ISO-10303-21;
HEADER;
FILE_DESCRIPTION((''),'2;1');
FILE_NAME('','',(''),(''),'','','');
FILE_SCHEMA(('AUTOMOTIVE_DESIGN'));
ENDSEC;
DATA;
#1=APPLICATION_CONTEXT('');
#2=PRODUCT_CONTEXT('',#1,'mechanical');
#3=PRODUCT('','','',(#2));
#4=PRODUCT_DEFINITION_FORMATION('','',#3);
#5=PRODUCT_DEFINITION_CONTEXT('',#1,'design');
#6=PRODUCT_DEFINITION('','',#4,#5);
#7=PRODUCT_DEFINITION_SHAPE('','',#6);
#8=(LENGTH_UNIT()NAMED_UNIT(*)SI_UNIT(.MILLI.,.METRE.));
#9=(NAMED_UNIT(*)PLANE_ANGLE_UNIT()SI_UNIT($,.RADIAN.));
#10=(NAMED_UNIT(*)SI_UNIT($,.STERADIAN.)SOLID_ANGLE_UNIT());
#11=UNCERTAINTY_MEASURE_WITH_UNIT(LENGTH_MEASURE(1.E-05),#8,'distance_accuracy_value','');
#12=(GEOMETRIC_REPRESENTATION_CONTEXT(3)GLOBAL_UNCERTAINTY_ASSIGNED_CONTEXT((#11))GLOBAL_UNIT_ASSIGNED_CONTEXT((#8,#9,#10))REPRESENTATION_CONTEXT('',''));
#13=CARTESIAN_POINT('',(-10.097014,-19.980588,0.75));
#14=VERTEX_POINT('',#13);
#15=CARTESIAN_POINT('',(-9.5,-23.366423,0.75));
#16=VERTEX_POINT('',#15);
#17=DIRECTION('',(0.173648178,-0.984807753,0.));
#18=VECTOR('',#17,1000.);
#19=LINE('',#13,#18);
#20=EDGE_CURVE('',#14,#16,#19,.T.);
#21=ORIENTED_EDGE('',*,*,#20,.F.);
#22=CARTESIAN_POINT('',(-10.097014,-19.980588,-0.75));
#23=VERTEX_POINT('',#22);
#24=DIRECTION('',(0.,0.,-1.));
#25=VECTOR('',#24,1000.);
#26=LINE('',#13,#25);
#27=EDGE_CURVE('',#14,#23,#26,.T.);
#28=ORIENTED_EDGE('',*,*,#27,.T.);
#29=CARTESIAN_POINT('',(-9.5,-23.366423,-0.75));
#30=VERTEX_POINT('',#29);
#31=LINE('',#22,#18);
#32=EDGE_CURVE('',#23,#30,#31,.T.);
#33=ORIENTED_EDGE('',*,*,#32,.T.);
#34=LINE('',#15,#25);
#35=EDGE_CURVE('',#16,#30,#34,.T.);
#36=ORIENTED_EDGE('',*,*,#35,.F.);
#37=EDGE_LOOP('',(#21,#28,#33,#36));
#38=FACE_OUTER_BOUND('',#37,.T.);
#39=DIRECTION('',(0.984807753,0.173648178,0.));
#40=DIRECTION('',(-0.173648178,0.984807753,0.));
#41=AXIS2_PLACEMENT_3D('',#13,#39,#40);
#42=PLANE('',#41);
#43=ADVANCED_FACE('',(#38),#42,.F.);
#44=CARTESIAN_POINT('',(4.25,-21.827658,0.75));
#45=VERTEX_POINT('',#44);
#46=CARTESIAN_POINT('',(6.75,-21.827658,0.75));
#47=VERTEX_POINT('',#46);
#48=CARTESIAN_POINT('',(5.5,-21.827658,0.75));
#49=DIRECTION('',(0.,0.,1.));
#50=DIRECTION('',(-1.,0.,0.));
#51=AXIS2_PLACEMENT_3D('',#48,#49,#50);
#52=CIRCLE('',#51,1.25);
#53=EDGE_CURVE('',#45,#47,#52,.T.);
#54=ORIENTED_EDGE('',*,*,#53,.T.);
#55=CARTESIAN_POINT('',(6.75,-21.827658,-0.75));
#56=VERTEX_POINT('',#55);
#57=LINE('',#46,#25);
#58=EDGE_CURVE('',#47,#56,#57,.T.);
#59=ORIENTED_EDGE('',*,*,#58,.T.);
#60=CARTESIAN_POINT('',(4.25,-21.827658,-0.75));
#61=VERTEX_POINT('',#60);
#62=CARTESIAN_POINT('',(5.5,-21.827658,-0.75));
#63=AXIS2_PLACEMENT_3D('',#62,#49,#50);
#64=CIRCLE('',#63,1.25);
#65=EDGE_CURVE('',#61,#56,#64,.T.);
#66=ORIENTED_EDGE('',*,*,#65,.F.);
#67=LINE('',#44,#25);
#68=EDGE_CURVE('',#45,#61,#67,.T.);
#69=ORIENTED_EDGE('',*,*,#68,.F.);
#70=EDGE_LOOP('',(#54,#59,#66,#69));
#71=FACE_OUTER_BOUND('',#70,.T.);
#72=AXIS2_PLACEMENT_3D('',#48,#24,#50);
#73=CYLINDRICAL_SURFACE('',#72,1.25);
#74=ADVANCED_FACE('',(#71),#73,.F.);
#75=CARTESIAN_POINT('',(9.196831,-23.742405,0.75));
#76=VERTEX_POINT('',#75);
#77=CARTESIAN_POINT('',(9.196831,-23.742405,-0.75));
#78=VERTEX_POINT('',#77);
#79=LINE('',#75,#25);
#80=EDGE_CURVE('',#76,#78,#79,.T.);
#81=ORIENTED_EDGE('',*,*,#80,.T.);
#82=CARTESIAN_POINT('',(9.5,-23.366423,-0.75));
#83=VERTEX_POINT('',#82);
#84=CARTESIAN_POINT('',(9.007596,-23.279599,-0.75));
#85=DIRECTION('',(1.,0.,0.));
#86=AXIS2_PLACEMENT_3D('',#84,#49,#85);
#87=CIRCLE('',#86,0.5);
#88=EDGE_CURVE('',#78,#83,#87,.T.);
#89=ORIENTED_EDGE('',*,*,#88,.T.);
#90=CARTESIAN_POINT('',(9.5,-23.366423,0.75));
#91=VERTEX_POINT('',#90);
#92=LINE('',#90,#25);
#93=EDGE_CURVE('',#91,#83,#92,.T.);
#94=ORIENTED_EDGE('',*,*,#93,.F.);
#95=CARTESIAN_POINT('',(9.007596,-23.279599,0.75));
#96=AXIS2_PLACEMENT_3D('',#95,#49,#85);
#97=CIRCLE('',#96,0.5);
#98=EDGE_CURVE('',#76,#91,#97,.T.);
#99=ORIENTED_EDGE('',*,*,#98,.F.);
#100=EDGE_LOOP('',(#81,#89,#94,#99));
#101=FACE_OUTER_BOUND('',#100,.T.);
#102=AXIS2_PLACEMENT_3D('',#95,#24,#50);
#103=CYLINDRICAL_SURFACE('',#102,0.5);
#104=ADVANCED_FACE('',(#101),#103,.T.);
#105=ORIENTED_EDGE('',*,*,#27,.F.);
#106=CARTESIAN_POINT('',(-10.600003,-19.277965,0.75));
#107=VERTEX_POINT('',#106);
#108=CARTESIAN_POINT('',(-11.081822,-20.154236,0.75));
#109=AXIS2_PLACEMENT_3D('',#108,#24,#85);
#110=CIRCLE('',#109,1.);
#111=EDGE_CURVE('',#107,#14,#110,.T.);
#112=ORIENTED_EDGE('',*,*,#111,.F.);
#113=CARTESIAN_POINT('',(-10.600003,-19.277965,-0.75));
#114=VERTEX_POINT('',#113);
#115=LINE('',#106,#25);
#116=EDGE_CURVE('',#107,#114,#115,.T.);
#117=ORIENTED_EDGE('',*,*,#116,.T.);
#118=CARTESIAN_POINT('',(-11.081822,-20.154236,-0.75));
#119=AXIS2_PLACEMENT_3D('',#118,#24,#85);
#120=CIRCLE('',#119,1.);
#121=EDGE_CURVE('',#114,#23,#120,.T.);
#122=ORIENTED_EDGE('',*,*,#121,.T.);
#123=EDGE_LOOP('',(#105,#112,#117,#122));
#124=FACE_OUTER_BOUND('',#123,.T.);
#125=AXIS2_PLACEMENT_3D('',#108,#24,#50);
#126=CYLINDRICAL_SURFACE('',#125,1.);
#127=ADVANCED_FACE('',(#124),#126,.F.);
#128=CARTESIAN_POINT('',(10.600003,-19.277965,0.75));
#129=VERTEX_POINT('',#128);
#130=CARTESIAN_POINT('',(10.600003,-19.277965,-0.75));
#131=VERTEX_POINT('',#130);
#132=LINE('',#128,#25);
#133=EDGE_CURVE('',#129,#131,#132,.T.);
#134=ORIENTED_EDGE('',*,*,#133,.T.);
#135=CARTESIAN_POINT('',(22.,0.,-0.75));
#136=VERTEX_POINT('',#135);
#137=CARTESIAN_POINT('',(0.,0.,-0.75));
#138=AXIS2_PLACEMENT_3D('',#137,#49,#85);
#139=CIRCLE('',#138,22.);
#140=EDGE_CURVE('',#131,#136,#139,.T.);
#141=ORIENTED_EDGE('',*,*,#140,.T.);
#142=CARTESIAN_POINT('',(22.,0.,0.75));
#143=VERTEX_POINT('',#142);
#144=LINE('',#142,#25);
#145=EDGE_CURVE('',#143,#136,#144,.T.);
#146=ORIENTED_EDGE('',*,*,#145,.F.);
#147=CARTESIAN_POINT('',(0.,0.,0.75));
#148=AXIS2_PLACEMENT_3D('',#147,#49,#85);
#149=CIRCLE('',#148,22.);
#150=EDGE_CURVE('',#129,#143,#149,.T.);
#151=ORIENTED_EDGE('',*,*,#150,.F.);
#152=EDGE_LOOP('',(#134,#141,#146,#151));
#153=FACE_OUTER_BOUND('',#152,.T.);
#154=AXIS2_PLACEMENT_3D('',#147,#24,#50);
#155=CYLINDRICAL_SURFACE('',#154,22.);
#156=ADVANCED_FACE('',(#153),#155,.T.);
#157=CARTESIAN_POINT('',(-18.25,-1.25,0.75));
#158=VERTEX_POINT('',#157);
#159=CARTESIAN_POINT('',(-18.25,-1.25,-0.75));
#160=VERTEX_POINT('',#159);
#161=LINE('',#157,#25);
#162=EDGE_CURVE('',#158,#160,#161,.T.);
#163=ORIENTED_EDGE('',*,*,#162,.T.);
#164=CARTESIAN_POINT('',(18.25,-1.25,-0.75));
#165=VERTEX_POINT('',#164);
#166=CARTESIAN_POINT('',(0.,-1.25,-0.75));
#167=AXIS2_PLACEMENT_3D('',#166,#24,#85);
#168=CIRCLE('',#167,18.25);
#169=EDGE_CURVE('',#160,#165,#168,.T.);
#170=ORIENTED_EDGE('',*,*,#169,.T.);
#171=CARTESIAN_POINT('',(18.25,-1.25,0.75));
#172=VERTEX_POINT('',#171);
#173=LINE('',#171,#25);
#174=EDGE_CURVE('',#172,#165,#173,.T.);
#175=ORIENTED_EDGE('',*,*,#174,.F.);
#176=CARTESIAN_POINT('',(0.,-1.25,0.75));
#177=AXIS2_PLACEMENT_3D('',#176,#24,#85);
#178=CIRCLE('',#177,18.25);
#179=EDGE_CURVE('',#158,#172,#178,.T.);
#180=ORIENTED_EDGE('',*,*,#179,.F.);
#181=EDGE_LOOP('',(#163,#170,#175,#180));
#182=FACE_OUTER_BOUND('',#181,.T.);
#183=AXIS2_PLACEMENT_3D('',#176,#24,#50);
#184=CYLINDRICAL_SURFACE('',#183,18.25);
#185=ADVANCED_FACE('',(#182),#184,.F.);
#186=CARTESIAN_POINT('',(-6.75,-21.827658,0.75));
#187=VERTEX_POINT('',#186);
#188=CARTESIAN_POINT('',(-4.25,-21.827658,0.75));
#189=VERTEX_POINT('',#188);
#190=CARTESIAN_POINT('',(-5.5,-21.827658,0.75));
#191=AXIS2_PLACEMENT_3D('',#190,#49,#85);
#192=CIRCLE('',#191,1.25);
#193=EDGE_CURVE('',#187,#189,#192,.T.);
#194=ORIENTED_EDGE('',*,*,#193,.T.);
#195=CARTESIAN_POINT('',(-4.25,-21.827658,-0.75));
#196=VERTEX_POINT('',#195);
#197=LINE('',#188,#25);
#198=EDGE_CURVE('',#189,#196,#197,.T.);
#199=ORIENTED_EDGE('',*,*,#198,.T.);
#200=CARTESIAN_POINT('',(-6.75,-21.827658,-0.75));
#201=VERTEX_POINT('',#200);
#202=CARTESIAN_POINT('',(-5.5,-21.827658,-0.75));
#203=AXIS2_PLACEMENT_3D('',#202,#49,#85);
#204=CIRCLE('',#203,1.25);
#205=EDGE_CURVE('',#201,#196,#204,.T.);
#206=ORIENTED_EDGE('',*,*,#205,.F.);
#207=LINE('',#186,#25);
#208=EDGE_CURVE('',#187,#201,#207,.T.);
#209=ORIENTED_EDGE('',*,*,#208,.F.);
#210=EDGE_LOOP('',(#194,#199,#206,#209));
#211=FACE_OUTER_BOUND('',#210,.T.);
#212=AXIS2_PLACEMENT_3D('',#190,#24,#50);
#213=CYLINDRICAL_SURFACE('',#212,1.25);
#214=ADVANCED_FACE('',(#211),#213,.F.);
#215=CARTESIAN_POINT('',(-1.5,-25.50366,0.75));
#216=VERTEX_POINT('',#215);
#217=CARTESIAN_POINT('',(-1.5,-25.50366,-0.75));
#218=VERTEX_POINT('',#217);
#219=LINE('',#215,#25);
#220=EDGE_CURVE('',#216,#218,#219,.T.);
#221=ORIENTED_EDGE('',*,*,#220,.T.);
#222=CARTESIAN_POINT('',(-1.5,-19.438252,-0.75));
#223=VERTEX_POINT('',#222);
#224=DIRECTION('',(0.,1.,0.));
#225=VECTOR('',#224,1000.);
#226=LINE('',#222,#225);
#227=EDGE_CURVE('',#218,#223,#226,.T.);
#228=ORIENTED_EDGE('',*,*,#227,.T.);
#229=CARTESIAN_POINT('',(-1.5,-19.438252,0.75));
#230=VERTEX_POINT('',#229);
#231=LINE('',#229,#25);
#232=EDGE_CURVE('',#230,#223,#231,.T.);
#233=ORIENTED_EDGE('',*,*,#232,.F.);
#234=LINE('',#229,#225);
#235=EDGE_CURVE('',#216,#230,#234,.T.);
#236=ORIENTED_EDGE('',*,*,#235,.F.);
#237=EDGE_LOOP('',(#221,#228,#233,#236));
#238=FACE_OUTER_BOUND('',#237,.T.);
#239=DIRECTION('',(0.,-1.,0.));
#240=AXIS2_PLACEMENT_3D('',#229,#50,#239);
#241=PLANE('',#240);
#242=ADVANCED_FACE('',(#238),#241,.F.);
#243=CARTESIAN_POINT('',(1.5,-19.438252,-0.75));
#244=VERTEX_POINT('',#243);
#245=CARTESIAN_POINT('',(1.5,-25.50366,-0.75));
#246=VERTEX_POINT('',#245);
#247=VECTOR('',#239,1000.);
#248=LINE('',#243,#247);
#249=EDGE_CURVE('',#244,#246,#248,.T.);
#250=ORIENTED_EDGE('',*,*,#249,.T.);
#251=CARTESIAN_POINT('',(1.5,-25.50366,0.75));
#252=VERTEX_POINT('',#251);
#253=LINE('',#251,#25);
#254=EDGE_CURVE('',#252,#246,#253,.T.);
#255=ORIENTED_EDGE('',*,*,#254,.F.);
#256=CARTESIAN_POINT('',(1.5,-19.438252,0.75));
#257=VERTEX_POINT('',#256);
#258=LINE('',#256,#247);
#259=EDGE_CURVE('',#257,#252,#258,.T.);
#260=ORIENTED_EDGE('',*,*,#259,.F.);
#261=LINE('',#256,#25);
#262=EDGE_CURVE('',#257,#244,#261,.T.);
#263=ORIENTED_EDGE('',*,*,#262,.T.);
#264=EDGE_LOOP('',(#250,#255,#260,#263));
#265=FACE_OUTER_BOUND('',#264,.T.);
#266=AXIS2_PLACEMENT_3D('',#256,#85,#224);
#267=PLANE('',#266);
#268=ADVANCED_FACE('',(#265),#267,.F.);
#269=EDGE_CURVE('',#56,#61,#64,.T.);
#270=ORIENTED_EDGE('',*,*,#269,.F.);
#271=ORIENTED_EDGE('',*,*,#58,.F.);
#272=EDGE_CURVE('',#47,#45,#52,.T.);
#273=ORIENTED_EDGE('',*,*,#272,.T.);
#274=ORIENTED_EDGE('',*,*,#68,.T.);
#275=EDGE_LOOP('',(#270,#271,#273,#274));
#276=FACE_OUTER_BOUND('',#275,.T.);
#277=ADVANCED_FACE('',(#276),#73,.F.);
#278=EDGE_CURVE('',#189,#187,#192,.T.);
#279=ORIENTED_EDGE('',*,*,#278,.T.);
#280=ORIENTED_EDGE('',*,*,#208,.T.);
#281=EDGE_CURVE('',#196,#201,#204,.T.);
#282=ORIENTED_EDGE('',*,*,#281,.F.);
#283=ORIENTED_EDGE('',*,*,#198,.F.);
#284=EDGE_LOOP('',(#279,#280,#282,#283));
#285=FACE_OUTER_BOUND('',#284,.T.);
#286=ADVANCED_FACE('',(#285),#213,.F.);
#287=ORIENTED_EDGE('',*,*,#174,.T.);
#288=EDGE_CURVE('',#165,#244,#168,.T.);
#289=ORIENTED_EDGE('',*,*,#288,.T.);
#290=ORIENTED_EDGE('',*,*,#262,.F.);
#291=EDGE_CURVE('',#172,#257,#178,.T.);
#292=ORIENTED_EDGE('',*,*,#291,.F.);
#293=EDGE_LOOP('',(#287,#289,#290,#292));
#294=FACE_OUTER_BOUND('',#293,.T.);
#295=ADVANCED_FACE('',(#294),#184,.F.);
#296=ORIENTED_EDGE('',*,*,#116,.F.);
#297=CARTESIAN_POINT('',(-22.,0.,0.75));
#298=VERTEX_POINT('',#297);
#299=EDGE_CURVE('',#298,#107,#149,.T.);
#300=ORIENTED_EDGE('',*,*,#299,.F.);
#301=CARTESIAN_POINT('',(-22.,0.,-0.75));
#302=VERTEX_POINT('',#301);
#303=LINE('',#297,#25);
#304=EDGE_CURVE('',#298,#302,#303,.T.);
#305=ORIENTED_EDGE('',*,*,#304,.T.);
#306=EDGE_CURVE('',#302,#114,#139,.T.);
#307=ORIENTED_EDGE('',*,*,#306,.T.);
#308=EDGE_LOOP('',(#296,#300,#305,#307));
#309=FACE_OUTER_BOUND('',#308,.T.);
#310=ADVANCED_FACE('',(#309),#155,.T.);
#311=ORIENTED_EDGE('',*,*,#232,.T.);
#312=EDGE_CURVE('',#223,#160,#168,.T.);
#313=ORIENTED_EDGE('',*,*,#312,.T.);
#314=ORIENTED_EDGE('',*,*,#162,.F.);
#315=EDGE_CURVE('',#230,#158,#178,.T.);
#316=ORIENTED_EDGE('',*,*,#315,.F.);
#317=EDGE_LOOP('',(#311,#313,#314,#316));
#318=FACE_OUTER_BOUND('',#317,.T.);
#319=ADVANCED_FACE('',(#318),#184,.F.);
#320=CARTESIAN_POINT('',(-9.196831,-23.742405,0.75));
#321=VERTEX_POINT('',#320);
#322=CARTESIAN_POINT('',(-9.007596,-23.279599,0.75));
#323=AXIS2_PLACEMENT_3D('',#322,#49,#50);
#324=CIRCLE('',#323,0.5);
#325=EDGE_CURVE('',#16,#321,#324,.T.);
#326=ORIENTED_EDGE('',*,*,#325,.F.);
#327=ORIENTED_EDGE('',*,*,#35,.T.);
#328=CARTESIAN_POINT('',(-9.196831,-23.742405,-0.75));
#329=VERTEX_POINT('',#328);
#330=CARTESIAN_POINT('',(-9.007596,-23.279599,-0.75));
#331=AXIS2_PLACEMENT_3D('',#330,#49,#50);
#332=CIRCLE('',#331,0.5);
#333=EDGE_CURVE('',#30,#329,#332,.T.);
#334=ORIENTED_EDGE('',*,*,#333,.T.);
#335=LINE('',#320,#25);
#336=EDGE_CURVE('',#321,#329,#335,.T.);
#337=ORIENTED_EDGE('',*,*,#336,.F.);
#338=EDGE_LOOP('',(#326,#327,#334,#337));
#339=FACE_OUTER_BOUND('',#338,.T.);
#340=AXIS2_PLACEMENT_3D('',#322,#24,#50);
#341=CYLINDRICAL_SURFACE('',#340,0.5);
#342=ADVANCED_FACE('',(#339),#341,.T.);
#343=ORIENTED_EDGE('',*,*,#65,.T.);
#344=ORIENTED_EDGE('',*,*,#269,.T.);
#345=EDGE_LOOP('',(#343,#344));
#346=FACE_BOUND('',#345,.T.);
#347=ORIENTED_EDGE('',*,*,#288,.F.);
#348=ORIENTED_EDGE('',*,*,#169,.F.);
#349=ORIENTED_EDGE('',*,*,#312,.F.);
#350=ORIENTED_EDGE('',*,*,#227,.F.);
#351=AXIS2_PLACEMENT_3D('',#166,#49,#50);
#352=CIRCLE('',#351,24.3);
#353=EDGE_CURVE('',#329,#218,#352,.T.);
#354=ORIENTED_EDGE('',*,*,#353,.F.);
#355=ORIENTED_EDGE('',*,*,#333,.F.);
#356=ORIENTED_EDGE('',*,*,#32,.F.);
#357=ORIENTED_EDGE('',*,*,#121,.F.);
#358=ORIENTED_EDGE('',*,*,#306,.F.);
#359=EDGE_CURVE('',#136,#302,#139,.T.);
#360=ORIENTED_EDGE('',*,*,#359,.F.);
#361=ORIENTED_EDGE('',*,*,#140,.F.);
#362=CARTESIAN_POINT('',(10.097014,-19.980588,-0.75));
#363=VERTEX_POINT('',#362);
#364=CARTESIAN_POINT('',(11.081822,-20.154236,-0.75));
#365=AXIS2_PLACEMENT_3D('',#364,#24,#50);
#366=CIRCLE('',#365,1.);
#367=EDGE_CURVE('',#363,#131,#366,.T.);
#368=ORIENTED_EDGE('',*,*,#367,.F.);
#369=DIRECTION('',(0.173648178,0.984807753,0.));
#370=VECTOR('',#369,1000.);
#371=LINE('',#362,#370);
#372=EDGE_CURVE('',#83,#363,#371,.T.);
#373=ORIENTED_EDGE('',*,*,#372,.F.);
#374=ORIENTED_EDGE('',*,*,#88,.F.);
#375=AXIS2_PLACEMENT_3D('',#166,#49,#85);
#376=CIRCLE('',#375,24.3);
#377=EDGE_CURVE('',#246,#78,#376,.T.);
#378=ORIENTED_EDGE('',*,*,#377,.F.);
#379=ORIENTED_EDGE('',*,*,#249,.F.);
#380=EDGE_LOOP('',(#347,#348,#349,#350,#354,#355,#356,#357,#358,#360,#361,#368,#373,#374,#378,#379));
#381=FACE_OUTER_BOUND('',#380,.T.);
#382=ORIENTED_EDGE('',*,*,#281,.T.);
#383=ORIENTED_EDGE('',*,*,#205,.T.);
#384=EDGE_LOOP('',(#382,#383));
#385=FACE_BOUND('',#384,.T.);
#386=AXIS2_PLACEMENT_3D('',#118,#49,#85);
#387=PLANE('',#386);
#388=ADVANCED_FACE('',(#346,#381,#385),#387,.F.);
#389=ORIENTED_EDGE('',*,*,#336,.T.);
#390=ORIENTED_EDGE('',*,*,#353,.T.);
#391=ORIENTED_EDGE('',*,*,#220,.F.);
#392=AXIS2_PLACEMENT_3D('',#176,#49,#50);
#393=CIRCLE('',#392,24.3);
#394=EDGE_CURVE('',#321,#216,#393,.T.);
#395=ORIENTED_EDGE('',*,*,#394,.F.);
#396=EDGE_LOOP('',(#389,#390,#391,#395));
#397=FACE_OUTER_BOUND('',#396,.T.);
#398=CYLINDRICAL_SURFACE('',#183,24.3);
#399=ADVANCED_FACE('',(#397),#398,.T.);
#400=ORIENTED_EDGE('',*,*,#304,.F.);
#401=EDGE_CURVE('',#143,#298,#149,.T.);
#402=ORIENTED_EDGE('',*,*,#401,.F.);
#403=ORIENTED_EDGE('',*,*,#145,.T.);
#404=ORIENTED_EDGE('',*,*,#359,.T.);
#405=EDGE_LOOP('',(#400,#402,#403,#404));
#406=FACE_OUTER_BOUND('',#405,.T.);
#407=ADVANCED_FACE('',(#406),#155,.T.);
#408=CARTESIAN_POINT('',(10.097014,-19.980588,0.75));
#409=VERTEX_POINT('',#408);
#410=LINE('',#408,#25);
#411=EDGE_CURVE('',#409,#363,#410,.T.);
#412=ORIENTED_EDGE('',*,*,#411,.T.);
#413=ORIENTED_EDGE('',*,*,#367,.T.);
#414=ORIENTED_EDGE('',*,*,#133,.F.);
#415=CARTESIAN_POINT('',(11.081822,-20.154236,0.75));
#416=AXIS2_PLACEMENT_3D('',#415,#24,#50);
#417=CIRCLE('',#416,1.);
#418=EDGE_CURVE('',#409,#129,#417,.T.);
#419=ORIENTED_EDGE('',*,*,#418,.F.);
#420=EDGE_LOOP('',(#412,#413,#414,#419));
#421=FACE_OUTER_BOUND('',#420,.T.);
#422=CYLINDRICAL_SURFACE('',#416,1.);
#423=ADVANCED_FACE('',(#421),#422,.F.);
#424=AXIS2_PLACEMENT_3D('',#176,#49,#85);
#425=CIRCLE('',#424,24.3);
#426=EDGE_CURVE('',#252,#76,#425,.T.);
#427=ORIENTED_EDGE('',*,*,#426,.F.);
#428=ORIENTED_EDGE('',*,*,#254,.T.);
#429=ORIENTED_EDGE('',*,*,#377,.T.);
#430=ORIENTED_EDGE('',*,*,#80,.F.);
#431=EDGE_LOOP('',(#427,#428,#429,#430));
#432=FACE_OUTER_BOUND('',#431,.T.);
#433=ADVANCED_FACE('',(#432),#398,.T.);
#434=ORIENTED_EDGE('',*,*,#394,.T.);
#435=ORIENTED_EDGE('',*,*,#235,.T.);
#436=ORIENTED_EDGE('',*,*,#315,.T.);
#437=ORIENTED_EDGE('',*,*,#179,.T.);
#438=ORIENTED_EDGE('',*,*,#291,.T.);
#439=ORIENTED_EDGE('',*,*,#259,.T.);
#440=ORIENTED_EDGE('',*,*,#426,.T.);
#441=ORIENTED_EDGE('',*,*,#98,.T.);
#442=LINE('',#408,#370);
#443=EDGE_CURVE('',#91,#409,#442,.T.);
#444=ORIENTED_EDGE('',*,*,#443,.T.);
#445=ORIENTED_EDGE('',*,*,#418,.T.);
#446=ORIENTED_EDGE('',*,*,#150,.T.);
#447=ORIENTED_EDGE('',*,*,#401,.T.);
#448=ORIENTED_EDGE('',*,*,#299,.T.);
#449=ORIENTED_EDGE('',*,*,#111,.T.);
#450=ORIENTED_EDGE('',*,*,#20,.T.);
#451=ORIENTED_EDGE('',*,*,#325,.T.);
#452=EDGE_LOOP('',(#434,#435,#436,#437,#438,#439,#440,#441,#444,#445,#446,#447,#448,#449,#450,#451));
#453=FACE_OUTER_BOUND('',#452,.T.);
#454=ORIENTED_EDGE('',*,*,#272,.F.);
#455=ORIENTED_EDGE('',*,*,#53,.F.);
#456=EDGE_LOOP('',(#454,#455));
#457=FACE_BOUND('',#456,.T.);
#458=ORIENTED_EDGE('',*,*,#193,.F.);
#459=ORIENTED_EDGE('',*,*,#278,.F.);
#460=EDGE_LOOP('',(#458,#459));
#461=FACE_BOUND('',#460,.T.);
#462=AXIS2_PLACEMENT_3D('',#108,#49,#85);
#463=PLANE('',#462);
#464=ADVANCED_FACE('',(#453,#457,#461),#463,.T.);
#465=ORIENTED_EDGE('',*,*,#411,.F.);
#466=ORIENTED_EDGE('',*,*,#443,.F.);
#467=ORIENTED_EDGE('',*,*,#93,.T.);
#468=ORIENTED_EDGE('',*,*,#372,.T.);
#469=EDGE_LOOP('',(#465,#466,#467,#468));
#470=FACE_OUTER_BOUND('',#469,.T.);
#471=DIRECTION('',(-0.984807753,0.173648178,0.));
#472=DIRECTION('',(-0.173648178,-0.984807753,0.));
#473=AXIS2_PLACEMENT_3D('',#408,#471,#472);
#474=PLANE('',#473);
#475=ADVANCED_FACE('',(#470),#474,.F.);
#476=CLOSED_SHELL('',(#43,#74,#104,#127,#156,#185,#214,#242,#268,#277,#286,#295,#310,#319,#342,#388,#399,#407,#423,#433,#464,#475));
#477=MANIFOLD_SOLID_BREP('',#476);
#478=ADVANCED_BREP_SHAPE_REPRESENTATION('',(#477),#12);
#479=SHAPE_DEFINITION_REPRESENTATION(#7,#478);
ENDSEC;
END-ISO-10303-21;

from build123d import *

# Parameters (mm, degrees)
EXTRUDE_972_DEPTH      = 0.75
EXTRUDE_972_DEPTH_BACK = 0.75
SKETCH_1_R             = 1.25


with BuildPart() as part:
    # 草图1 → Extrude 972 (new, two sides: drawn at the far end of the back side and taken through both)
    with BuildSketch(Plane.XY.offset(-EXTRUDE_972_DEPTH_BACK)):
        with BuildLine():
            Line((-1.5, -19.438251703), (-1.5, -25.503659518))
            ThreePointArc((-1.5, -25.503659518), (-5.420429348, -24.937738298), (-9.196831336, -23.742405238))
            ThreePointArc((-9.196831336, -23.742405238), (-9.396824452, -23.593447727), (-9.5, -23.366422634))
            Line((-9.5, -23.366422634), (-10.097014043, -19.980587746))
            ThreePointArc((-10.097014043, -19.980587746), (-10.268699557, -19.572142955), (-10.600003457, -19.277964797))
            ThreePointArc((-10.600003457, -19.277964797), (0, 22), (10.600003457, -19.277964797))
            ThreePointArc((10.600003457, -19.277964797), (10.268699557, -19.572142955), (10.097014043, -19.980587746))
            Line((10.097014043, -19.980587746), (9.5, -23.366422634))
            ThreePointArc((9.5, -23.366422634), (9.396824452, -23.593447727), (9.196831336, -23.742405238))
            ThreePointArc((9.196831336, -23.742405238), (5.420429348, -24.937738298), (1.5, -25.503659518))
            Line((1.5, -25.503659518), (1.5, -19.438251703))
            ThreePointArc((1.5, -19.438251703), (0, 17), (-1.5, -19.438251703))
        make_face()
        with Locations((-5.5, -21.827657787)):
            Circle(SKETCH_1_R, mode=Mode.SUBTRACT)
        with Locations(Location((5.5, -21.827657787, 0), (0, 0, 180))):
            Circle(SKETCH_1_R, mode=Mode.SUBTRACT)
    extrude(amount=EXTRUDE_972_DEPTH + EXTRUDE_972_DEPTH_BACK)


solid = part.part
